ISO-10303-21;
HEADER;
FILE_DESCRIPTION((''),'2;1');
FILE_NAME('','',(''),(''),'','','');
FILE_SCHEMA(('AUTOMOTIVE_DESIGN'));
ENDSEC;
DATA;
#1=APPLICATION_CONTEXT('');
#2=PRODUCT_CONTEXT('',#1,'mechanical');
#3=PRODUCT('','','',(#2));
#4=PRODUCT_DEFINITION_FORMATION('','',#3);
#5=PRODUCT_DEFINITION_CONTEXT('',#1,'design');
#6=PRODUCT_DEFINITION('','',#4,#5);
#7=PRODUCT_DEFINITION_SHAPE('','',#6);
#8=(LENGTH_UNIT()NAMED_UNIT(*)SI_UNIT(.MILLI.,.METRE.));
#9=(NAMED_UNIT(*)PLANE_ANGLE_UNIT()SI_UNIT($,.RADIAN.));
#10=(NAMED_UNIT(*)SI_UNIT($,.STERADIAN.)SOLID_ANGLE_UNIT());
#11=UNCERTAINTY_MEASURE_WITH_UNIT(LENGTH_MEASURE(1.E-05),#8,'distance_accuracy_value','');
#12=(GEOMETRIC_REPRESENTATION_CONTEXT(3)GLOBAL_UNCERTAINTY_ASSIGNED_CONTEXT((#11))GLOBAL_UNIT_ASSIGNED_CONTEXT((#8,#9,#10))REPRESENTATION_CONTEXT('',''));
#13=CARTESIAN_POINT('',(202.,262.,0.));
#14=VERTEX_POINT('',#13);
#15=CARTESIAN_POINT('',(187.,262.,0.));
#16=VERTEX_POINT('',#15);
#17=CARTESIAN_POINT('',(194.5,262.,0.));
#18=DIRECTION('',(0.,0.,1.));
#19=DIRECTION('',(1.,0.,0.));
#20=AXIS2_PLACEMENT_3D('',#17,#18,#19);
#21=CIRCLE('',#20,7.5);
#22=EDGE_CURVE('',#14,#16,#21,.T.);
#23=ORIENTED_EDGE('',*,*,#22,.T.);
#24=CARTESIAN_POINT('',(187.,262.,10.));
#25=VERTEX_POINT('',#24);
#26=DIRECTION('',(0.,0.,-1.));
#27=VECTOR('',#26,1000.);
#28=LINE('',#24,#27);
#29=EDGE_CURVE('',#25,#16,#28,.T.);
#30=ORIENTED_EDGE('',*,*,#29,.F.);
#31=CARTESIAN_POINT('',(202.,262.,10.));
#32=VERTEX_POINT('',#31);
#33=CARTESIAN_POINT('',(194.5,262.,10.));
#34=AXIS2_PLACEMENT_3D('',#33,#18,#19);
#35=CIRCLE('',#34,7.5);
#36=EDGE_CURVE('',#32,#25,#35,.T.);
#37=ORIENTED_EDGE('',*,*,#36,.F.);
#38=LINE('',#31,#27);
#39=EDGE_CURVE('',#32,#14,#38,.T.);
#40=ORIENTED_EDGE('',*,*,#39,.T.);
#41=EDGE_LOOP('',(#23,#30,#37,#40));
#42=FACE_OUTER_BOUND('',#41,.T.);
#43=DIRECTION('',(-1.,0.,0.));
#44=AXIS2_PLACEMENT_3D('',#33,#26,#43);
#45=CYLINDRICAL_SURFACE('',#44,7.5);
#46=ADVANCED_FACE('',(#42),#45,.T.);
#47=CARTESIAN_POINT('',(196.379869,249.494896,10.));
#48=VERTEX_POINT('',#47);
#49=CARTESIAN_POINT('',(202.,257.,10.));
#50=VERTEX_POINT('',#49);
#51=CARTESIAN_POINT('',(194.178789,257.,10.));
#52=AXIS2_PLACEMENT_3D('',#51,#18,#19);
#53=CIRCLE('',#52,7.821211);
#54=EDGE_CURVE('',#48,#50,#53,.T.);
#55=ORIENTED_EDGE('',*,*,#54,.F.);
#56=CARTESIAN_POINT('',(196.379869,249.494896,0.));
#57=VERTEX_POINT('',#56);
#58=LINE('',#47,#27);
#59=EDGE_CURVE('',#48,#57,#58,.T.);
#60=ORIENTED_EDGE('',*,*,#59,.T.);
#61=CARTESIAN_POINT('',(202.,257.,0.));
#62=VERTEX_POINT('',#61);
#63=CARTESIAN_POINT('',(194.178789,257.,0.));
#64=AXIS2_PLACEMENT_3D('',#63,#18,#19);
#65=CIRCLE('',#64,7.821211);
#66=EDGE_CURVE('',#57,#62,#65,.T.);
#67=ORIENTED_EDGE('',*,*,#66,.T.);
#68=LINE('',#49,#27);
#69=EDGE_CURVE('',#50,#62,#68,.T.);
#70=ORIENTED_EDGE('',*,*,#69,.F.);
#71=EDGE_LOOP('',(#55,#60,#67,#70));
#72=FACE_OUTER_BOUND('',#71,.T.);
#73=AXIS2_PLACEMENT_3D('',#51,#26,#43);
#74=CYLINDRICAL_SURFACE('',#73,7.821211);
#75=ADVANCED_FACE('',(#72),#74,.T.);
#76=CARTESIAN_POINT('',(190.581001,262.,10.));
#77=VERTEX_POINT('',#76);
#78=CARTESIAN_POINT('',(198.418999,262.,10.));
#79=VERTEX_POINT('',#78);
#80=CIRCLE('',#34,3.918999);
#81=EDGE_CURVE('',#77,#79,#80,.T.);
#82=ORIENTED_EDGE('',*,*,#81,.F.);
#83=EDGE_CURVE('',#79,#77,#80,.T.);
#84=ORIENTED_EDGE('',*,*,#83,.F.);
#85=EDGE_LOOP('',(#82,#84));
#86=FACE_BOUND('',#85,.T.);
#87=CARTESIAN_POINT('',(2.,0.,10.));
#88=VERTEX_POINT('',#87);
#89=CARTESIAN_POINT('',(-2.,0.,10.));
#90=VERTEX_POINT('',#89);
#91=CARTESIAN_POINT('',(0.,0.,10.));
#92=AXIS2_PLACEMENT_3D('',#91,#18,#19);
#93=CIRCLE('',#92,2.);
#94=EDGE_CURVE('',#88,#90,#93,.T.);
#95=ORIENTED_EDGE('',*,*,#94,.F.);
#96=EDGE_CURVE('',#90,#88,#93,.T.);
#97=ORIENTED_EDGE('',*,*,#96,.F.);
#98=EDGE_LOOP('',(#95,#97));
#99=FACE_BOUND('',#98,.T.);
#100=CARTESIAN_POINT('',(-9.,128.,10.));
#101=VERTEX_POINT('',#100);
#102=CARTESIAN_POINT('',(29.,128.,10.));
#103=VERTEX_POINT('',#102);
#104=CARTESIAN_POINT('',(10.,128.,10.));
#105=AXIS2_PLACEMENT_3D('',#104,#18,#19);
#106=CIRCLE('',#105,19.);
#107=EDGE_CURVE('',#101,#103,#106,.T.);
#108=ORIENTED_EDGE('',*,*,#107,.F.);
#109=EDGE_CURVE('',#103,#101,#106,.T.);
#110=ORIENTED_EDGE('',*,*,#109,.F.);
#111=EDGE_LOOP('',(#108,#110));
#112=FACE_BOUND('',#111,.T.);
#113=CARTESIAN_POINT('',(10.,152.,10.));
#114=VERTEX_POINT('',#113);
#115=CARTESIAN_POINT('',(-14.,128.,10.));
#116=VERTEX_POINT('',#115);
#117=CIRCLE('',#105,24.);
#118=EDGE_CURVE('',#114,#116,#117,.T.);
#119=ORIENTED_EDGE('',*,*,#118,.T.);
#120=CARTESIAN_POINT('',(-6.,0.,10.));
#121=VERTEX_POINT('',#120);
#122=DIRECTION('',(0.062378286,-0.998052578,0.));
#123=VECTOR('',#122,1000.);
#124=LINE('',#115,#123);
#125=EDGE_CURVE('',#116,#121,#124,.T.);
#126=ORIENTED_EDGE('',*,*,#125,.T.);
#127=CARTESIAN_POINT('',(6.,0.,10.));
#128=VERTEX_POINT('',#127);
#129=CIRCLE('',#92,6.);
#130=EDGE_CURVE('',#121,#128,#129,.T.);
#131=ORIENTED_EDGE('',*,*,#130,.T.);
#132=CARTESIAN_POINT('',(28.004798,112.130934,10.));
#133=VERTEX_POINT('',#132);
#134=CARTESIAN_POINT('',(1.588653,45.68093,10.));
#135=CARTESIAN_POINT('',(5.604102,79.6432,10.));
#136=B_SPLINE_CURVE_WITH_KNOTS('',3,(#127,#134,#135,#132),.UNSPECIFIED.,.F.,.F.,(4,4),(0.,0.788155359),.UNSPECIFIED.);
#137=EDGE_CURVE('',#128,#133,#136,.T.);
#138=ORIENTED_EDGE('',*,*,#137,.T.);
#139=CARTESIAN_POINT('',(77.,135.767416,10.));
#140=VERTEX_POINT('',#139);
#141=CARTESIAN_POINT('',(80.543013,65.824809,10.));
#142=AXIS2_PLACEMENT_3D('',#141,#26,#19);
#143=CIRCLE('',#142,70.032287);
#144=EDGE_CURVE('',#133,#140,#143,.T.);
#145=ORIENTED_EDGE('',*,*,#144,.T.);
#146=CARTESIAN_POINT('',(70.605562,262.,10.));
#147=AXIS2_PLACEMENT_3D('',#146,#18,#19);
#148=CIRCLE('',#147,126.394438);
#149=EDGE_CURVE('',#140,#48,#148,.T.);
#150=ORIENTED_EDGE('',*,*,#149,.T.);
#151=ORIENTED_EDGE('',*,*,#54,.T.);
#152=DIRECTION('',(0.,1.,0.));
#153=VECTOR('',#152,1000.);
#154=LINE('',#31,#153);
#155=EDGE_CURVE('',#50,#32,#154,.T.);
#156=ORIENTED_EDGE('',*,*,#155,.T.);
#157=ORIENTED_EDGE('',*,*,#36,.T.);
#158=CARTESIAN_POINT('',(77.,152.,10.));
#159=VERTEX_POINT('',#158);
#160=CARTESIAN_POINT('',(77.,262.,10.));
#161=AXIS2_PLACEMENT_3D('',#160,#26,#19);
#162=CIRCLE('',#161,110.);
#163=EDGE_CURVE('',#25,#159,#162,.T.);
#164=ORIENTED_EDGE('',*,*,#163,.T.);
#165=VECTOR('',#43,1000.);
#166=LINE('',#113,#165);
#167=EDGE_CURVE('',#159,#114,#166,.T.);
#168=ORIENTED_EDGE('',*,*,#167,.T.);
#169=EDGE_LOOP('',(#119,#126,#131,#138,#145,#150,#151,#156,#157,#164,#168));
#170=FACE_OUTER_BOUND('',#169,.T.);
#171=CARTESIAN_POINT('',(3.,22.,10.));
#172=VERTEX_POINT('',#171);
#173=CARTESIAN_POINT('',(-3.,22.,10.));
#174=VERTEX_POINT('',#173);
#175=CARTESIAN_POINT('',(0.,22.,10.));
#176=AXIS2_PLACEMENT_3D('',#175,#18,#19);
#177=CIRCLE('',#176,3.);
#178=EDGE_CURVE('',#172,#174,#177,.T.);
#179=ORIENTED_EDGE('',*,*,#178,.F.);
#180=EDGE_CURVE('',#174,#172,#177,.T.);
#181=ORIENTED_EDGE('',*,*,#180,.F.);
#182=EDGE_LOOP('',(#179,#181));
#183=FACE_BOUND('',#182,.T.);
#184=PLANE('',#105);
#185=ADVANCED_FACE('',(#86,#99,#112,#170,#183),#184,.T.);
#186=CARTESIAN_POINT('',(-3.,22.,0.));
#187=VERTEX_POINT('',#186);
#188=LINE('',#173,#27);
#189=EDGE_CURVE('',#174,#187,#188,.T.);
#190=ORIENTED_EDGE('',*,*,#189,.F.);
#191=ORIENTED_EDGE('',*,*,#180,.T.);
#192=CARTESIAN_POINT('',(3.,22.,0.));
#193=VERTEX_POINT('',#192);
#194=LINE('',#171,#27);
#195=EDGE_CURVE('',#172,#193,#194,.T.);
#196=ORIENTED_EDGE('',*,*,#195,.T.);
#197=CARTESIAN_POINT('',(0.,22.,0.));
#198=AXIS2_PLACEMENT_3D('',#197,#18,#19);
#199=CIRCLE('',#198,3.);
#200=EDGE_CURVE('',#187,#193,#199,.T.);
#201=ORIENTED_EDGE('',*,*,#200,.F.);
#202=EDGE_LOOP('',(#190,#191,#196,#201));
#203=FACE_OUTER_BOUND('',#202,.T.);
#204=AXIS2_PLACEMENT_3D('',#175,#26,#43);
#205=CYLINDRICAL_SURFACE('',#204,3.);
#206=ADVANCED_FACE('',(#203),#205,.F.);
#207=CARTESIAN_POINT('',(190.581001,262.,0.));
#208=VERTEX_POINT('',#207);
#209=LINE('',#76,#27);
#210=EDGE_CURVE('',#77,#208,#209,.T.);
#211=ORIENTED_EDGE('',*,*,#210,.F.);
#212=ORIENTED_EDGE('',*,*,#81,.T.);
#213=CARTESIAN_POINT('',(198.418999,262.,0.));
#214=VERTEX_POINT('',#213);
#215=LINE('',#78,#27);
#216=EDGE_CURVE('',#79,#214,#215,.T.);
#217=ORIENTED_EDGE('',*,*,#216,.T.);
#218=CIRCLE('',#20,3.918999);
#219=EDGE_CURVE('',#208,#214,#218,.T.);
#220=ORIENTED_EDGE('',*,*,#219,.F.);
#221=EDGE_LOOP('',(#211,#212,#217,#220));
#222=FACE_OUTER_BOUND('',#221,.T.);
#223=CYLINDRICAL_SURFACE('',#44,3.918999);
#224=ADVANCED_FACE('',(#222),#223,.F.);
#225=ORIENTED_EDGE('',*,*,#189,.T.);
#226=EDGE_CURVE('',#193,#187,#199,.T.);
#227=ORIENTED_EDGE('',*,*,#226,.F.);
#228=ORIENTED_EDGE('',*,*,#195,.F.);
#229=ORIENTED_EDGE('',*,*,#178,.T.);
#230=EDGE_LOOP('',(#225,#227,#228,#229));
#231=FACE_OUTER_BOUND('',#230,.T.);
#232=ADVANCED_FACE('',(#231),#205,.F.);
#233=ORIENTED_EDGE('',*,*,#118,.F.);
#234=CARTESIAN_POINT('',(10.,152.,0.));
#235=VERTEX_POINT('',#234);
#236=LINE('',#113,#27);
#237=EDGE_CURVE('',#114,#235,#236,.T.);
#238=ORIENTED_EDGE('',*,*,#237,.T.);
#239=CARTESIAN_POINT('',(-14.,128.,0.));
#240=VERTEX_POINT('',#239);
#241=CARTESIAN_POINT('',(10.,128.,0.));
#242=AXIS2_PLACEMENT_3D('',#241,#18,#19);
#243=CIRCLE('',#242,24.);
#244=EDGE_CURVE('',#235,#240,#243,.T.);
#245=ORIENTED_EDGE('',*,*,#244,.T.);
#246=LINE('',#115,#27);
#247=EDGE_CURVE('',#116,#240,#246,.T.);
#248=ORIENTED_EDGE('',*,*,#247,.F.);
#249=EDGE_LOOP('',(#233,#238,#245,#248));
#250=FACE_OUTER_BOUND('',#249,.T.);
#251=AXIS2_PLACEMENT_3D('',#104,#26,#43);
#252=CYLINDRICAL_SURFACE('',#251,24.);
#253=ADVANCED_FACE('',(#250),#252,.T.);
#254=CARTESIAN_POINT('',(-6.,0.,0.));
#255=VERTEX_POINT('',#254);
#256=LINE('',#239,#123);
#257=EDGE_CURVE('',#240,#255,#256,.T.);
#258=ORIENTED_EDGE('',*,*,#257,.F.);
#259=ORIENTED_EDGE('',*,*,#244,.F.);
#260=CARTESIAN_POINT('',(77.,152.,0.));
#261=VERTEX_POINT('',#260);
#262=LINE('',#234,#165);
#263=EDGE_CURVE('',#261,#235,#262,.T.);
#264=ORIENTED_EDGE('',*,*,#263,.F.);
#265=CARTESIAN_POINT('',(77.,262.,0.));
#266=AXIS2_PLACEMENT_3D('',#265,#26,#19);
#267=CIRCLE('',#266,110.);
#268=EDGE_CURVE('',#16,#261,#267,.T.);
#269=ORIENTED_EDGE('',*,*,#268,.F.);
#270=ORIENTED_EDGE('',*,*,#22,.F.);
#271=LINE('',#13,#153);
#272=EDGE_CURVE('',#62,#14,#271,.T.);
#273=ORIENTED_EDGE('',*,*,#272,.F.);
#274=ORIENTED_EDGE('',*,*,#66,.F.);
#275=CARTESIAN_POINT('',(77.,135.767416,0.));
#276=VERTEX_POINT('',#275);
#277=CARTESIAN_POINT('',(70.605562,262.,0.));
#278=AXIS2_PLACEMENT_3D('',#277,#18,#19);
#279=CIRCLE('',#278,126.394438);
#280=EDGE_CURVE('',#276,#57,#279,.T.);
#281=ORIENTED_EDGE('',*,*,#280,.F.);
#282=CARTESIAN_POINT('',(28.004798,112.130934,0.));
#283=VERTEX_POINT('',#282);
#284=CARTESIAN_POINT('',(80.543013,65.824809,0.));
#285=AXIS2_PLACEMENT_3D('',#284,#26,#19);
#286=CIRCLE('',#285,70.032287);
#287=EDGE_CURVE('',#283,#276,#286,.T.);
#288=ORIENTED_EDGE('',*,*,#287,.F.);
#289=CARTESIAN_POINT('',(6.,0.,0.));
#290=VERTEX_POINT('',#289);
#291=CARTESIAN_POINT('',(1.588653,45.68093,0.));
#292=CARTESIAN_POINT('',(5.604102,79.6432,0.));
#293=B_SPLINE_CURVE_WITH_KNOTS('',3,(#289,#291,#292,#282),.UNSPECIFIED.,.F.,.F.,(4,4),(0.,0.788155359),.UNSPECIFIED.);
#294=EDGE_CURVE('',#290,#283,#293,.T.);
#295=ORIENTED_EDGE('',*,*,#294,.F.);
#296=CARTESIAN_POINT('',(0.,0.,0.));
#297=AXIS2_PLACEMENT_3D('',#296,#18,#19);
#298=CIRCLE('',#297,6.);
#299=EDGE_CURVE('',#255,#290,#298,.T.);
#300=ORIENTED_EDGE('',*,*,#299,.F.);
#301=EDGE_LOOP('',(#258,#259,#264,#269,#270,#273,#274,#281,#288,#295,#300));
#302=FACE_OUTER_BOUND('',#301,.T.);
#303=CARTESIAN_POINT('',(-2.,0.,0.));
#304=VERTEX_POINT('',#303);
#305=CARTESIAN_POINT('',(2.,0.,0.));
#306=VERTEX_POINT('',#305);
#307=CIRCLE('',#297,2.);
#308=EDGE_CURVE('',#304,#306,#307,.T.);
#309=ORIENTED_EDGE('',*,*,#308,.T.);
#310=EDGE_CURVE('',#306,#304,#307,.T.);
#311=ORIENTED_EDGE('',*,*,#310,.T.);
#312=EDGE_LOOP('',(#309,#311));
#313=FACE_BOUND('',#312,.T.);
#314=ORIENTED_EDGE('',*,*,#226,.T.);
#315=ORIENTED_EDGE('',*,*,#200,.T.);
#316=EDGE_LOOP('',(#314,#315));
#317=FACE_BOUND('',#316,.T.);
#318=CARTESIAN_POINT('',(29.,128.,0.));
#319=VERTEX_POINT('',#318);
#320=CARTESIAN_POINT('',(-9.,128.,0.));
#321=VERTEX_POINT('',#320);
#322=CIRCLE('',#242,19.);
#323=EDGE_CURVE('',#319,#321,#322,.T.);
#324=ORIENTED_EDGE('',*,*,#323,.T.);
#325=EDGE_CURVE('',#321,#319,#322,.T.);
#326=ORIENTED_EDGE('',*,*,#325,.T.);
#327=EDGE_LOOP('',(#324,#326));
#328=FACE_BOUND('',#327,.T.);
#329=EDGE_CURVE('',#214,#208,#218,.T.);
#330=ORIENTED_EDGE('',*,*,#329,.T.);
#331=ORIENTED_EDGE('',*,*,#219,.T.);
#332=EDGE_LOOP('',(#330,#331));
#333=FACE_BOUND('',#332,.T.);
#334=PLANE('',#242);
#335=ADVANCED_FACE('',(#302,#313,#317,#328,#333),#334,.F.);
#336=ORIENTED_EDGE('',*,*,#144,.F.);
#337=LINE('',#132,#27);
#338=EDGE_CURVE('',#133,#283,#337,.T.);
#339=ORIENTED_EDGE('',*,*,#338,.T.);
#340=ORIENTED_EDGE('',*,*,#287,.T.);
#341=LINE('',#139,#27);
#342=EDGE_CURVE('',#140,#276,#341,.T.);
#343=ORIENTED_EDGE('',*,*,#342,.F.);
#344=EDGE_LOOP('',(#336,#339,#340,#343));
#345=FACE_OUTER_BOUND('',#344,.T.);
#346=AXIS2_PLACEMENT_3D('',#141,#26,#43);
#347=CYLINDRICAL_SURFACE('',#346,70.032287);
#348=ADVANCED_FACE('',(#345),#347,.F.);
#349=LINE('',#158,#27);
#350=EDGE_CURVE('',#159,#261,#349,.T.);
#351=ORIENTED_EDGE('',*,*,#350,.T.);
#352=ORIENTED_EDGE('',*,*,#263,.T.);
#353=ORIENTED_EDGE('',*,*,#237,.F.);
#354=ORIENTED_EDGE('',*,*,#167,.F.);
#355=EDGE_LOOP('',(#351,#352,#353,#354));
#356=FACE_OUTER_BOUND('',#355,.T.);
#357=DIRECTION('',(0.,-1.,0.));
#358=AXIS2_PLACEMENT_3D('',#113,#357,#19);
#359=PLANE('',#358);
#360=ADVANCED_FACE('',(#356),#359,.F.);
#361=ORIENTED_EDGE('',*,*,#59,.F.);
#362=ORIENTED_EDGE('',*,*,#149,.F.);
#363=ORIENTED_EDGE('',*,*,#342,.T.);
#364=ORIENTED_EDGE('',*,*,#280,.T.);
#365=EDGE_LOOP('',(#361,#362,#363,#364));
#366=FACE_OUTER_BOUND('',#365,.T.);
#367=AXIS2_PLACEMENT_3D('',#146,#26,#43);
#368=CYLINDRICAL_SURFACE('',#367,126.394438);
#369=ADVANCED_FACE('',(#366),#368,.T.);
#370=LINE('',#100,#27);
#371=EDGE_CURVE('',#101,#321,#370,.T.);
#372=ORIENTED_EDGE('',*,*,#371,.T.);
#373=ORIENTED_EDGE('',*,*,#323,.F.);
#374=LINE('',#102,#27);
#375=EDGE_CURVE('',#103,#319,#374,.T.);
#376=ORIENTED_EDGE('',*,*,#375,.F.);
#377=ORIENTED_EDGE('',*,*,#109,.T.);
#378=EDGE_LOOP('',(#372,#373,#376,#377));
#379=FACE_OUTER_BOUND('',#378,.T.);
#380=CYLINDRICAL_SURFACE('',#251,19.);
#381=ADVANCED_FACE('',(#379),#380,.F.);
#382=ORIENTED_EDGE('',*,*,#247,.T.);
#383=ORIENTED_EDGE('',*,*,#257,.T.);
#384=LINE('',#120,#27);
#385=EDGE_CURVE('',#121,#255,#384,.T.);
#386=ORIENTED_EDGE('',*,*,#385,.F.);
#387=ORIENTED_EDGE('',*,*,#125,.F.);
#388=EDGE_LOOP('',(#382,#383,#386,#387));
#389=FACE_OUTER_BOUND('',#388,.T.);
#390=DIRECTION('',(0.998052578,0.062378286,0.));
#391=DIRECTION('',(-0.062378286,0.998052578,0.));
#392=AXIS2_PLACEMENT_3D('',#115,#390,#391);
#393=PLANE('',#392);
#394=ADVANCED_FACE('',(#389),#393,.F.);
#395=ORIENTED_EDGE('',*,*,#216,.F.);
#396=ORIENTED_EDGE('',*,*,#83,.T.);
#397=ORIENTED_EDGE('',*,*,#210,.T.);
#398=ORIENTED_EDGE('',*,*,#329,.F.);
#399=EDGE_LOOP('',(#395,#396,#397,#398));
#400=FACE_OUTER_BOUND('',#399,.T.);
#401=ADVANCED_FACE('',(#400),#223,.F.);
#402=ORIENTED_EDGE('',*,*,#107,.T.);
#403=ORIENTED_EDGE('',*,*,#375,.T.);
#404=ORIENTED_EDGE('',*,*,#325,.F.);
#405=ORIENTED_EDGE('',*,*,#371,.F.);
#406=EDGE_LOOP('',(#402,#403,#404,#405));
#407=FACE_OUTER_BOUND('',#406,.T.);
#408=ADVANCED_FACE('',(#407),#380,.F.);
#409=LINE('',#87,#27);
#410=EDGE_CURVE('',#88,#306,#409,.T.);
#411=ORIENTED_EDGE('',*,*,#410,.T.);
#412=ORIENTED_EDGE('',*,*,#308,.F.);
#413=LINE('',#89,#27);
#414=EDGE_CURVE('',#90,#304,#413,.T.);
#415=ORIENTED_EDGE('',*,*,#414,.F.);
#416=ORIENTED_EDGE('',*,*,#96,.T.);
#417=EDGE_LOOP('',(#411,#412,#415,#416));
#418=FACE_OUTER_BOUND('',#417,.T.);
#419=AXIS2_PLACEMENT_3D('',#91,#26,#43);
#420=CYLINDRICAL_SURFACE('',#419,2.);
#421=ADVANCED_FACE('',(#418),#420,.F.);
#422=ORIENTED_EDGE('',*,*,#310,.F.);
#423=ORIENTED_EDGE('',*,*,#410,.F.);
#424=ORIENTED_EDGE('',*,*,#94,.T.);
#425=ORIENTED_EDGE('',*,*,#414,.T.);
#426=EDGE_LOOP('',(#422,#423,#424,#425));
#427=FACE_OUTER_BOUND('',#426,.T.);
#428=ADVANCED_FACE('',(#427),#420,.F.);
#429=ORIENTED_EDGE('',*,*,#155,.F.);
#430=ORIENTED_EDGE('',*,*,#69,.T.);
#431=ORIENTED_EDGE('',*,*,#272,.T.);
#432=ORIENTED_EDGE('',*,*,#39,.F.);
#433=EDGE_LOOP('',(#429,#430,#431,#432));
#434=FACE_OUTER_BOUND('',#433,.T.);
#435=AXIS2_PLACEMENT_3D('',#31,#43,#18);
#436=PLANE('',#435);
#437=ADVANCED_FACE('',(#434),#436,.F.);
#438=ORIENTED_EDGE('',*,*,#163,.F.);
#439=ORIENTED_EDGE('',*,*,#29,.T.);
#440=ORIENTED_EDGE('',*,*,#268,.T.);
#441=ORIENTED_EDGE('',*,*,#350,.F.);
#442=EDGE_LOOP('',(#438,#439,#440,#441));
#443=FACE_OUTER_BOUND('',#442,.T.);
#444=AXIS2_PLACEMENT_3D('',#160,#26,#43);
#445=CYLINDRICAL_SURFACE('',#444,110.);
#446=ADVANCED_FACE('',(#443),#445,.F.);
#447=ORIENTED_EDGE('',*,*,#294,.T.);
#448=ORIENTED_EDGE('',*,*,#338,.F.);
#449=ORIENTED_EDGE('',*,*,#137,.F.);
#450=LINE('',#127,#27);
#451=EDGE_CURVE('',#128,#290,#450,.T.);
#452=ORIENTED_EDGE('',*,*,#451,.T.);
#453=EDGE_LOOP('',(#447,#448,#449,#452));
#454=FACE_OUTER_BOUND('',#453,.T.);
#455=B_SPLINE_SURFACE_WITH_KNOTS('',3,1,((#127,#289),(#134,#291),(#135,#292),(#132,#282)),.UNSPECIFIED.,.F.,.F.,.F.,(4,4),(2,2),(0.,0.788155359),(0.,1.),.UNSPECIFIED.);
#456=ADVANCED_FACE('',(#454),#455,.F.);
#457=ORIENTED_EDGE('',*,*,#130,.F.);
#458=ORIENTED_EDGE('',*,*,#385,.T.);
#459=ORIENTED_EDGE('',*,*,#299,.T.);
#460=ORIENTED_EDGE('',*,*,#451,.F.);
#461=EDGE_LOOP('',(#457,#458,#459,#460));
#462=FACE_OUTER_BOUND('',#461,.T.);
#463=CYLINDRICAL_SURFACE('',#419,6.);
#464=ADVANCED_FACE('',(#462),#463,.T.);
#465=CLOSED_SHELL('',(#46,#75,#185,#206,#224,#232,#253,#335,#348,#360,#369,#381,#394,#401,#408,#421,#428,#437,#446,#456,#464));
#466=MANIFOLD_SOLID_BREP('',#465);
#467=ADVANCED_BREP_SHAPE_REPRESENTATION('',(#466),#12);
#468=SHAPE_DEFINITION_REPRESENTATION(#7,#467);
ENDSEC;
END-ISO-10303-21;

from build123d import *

# Parameters (mm, degrees)
SKETCH_1_R      = 2
SKETCH_1_R_2    = 19
SKETCH_1_R_3    = 3.91899873
SKETCH_1_R_4    = 3
EXTRUDE_3_DEPTH = 10


with BuildPart() as part:
    # 草图1 → 凸台-拉伸3 (new body)
    with BuildSketch(Plane.XY):
        with BuildLine():
            Line((-14, 128), (-6, 0))
            ThreePointArc((-6, 0), (0, -6), (6, 0))
            add(Edge.make_bspline(
                [(6, 0), (1.588652615, 45.680929706), (5.604102499, 79.643200211), (28.004797731, 112.13093391)],
                knots=[0, 0, 0, 0, 0.788155359, 0.788155359, 0.788155359, 0.788155359], degree=3))
            ThreePointArc((28.004797731, 112.13093391), (50.113637924, 128.900750568), (77, 135.767416406))
            ThreePointArc((77, 135.767416406), (157.787149523, 170.485384951), (196.379869136, 249.494896157))
            ThreePointArc((196.379869136, 249.494896157), (200.439238403, 252.311917913), (202, 257))
            Line((202, 257), (202, 262))
            ThreePointArc((202, 262), (194.5, 269.5), (187, 262))
            ThreePointArc((187, 262), (154.781745931, 184.218254069), (77, 152))
            Line((77, 152), (10, 152))
            ThreePointArc((10, 152), (-6.970562748, 144.970562748), (-14, 128))
        make_face()
        Circle(SKETCH_1_R, mode=Mode.SUBTRACT)
        with Locations((10, 128)):
            Circle(SKETCH_1_R_2, mode=Mode.SUBTRACT)
        with Locations((194.5, 262)):
            Circle(SKETCH_1_R_3, mode=Mode.SUBTRACT)
        with Locations((0, 22)):
            Circle(SKETCH_1_R_4, mode=Mode.SUBTRACT)
    extrude(amount=EXTRUDE_3_DEPTH)


solid = part.part
